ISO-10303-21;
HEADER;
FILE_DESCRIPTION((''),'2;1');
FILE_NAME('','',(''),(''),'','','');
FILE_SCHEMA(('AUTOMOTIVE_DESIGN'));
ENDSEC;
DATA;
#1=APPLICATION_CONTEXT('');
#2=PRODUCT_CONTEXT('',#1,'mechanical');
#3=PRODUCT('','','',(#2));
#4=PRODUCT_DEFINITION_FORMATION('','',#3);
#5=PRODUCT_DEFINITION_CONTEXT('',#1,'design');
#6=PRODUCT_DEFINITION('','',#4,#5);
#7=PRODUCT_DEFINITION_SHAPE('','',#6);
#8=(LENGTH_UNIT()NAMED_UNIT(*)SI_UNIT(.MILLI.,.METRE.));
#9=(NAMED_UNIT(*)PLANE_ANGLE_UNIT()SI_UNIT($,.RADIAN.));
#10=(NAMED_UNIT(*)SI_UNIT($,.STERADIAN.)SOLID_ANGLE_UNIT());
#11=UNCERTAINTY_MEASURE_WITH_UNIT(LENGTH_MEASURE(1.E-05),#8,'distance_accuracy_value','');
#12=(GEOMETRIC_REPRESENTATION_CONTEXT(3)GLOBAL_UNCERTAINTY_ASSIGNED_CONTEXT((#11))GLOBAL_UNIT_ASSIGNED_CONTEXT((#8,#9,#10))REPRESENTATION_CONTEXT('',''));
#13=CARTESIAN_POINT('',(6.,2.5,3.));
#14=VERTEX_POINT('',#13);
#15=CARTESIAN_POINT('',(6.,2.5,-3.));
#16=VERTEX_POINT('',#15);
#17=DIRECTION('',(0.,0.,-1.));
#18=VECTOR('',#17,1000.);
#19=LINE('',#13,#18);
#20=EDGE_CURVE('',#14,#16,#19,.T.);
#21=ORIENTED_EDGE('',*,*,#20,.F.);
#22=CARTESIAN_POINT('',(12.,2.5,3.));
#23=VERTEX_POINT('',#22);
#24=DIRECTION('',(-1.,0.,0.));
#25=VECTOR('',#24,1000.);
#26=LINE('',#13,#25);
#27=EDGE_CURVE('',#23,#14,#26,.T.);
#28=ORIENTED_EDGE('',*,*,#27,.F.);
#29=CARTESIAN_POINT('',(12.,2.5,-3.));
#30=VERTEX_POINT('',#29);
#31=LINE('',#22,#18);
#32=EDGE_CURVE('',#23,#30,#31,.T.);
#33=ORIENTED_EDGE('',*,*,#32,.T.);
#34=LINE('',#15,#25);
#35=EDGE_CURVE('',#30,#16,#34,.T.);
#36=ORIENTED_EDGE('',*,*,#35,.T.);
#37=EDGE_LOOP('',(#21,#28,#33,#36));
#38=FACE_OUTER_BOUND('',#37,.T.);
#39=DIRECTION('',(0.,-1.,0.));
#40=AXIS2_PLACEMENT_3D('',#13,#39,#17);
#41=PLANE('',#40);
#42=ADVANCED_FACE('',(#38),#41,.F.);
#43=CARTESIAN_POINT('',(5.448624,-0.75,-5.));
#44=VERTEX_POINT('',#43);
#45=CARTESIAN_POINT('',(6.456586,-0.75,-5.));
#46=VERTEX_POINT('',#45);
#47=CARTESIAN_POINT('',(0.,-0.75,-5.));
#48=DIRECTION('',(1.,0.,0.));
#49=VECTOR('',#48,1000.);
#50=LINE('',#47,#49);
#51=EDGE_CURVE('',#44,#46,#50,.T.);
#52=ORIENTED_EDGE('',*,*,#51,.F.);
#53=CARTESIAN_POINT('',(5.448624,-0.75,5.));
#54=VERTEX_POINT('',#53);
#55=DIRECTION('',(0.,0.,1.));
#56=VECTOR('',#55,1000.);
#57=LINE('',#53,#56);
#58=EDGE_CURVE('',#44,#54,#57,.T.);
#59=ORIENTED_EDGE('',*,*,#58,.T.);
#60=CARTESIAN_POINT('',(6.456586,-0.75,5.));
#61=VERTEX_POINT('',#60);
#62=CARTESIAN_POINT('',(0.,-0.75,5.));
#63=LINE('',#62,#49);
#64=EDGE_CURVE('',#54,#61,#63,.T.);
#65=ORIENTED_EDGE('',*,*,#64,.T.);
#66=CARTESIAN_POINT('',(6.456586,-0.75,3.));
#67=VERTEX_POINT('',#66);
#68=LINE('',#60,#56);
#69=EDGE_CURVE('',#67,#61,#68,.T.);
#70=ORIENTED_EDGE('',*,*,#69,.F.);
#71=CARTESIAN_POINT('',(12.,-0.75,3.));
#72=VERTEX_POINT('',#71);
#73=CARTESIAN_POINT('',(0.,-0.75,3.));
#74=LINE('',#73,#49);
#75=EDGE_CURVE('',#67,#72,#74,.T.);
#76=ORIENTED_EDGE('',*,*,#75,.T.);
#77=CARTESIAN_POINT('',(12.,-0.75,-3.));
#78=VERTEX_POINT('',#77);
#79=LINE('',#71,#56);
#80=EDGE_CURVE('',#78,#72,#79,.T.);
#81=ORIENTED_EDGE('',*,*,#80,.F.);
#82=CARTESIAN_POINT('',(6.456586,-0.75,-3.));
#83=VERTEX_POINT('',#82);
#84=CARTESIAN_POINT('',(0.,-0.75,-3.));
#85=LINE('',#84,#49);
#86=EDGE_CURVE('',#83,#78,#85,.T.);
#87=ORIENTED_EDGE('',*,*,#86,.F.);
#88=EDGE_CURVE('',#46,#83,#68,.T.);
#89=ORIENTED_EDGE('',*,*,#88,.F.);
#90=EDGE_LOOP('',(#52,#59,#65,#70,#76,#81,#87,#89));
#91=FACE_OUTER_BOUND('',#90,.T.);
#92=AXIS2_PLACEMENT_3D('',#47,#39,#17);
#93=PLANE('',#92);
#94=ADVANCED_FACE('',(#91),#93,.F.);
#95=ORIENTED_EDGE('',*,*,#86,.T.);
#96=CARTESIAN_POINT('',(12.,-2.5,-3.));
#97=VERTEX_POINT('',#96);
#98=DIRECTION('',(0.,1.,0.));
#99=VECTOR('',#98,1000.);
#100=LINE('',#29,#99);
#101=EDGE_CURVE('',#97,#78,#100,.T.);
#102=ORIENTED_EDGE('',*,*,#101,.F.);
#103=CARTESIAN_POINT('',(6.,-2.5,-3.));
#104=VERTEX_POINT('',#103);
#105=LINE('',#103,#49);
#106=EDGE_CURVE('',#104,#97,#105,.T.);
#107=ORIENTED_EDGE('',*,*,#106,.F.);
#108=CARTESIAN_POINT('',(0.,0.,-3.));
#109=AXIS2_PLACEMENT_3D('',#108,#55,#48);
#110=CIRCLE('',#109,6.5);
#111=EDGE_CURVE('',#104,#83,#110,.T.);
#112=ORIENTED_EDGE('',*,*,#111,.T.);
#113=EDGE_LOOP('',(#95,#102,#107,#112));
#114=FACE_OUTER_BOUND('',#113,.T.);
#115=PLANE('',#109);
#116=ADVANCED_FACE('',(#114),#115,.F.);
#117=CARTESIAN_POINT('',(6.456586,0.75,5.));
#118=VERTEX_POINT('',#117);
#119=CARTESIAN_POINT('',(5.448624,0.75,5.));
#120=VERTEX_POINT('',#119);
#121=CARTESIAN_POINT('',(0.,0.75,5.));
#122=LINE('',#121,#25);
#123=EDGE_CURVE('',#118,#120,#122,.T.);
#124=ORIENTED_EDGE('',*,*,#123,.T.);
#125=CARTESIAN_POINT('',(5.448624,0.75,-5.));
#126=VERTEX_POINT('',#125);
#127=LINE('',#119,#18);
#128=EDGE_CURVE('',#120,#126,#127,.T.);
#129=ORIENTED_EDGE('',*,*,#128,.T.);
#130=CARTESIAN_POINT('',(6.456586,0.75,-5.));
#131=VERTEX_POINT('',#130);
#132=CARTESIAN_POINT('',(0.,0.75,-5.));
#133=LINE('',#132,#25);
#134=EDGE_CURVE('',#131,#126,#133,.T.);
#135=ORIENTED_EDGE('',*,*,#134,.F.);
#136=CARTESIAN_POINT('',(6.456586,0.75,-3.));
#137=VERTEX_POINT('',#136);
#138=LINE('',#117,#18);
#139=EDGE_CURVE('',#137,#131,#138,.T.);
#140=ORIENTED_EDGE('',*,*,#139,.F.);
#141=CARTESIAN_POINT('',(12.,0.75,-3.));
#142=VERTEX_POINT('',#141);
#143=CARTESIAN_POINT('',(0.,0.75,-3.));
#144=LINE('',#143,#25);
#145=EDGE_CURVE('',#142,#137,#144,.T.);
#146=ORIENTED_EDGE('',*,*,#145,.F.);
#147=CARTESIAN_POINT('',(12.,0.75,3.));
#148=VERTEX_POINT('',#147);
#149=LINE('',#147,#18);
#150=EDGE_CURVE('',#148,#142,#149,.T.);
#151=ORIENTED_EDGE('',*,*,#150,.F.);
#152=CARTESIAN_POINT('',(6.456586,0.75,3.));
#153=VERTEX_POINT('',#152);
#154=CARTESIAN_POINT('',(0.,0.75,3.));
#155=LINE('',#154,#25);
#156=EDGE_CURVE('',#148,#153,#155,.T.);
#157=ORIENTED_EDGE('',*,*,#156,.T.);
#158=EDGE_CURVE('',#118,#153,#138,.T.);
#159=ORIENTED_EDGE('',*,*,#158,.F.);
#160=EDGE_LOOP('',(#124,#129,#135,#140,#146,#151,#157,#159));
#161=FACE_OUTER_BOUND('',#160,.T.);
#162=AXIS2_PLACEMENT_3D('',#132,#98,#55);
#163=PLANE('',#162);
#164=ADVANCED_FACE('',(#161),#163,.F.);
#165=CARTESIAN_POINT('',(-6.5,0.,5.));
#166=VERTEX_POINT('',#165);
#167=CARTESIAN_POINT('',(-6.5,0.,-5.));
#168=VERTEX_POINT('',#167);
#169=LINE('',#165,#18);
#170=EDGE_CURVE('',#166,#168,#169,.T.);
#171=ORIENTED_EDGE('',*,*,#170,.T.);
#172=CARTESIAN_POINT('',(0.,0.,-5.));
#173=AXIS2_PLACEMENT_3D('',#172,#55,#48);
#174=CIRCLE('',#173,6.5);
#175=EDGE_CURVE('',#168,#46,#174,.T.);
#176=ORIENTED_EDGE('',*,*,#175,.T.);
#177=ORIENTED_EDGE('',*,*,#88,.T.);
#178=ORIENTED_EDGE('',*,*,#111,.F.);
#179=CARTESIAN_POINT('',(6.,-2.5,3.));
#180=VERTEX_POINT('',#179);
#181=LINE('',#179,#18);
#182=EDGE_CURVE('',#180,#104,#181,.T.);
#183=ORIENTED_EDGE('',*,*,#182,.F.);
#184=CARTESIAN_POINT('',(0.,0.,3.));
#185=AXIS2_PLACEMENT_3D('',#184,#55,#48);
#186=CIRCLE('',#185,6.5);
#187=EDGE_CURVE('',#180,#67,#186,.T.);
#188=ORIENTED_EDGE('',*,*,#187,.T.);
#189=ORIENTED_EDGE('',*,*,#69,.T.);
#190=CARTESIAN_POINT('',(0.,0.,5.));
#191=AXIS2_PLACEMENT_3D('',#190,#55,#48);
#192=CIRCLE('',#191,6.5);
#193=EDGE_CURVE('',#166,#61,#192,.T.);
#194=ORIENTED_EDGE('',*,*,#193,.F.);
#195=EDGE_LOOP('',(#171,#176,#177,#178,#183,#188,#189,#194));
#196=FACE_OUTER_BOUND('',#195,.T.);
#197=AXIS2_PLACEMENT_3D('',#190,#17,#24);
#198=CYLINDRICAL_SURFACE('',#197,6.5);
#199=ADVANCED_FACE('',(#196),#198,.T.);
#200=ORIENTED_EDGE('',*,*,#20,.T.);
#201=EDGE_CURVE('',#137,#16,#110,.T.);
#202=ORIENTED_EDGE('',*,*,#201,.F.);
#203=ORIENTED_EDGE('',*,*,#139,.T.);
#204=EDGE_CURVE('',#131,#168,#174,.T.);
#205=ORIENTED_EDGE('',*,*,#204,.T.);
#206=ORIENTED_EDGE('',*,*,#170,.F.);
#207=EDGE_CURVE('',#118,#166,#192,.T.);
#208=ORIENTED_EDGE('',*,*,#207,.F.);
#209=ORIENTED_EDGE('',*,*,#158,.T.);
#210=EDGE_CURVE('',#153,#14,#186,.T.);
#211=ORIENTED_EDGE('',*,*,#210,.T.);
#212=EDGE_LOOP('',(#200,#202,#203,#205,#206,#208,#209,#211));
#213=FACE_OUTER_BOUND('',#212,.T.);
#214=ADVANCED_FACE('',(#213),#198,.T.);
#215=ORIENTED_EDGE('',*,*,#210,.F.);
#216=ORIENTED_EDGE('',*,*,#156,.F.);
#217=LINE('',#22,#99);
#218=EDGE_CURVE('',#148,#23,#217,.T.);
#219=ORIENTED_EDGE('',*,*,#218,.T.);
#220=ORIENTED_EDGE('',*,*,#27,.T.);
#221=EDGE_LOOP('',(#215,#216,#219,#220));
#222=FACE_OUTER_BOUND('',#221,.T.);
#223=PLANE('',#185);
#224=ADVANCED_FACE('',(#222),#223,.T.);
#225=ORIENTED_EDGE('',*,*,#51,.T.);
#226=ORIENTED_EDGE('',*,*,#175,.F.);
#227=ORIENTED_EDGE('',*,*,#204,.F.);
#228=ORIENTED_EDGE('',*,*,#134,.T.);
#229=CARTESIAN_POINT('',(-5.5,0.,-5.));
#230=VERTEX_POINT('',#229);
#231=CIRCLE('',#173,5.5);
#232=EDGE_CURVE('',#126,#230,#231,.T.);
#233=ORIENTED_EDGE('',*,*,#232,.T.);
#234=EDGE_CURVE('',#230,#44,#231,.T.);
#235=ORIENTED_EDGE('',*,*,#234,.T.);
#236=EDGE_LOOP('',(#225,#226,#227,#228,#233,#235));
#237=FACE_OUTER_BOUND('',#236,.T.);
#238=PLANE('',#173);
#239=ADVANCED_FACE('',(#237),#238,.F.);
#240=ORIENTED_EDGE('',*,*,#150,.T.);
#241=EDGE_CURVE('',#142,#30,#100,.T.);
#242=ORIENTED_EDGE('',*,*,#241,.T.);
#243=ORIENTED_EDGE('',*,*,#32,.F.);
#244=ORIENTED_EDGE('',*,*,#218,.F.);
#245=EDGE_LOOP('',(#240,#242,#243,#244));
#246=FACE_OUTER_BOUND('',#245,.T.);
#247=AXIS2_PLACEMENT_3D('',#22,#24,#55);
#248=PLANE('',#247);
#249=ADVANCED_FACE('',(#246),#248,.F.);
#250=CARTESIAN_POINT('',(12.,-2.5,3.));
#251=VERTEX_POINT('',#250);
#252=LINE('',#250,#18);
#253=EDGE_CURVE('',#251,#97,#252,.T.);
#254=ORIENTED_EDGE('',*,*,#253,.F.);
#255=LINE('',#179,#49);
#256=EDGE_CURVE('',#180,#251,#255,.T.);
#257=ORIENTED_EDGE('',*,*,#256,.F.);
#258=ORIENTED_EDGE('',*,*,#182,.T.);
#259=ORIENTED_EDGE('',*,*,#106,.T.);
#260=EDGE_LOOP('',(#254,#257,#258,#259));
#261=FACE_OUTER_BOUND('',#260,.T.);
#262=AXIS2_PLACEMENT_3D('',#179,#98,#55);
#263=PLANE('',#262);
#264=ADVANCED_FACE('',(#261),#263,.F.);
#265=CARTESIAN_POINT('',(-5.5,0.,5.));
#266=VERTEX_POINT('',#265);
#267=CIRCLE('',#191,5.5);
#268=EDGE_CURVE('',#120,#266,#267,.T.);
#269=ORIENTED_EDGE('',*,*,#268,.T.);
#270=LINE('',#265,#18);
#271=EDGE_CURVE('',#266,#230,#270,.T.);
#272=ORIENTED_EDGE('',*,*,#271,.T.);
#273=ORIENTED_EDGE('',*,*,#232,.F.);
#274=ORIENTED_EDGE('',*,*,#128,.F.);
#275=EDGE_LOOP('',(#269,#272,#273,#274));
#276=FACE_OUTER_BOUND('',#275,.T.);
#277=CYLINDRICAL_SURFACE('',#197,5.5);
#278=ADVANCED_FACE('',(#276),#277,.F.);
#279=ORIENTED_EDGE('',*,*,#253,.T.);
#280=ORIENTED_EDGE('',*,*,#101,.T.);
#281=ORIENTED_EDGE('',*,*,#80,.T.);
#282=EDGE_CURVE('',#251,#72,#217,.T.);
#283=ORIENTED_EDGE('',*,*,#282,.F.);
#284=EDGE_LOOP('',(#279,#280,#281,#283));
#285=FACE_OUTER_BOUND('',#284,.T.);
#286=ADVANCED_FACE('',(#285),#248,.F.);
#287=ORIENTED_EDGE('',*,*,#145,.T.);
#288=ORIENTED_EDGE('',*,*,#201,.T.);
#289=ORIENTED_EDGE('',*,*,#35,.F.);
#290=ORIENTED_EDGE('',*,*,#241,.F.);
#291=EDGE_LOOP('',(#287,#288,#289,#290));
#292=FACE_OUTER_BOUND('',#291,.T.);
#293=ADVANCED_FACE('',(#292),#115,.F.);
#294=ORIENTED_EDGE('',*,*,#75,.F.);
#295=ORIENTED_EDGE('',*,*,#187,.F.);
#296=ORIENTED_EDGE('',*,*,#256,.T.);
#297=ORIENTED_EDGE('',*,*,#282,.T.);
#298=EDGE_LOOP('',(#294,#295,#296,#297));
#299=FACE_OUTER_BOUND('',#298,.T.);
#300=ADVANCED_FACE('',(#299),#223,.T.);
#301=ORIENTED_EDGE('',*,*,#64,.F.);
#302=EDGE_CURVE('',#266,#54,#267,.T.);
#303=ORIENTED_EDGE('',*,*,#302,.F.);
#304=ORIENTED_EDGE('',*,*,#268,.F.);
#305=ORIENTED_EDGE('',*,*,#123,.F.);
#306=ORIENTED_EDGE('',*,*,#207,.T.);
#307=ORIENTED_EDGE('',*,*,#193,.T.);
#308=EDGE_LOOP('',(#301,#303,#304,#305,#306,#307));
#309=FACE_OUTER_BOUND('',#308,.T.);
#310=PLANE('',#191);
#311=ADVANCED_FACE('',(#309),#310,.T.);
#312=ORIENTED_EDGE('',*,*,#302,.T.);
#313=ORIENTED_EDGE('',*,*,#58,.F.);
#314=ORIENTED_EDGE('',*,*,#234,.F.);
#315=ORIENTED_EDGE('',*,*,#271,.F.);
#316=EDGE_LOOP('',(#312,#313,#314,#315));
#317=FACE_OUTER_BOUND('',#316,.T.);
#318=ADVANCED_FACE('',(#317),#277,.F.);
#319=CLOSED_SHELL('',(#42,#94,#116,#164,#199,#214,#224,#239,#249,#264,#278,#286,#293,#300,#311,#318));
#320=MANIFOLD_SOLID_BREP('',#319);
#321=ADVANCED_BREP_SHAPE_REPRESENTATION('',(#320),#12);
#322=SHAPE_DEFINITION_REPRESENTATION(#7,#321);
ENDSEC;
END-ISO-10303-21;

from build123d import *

# Parameters (mm, degrees)
SKETCH1_R           = 6.5
SKETCH1_R_2         = 5.5
EXTRUDE_THIN1_DEPTH = 5
SKETCH2_W           = 6
SKETCH2_H           = 5
BOSS_EXTRUDE1_DEPTH = 3
SKETCH4_W           = 14.223079102
SKETCH4_H           = 1.5
CUT_EXTRUDE1_DEPTH  = 17.918924316


with BuildPart() as part:
    # Sketch1 → Extrude-Thin1 (new, symmetric)
    with BuildSketch(Plane.XY):
        Circle(SKETCH1_R)
        Circle(SKETCH1_R_2, mode=Mode.SUBTRACT)
    extrude(amount=EXTRUDE_THIN1_DEPTH, both=True)

    # Sketch2 → Boss-Extrude1 (add, symmetric)
    with BuildSketch(Plane.XY):
        with Locations((9, 0)):
            Rectangle(SKETCH2_W, SKETCH2_H)
    extrude(amount=BOSS_EXTRUDE1_DEPTH, both=True)

    # Sketch4 → Cut-Extrude1 (cut, through all)
    with BuildSketch(Plane.XY.offset(5)):
        with Locations((7.111539551, 0)):
            Rectangle(SKETCH4_W, SKETCH4_H)
    extrude(amount=-CUT_EXTRUDE1_DEPTH, mode=Mode.SUBTRACT)


solid = part.part
